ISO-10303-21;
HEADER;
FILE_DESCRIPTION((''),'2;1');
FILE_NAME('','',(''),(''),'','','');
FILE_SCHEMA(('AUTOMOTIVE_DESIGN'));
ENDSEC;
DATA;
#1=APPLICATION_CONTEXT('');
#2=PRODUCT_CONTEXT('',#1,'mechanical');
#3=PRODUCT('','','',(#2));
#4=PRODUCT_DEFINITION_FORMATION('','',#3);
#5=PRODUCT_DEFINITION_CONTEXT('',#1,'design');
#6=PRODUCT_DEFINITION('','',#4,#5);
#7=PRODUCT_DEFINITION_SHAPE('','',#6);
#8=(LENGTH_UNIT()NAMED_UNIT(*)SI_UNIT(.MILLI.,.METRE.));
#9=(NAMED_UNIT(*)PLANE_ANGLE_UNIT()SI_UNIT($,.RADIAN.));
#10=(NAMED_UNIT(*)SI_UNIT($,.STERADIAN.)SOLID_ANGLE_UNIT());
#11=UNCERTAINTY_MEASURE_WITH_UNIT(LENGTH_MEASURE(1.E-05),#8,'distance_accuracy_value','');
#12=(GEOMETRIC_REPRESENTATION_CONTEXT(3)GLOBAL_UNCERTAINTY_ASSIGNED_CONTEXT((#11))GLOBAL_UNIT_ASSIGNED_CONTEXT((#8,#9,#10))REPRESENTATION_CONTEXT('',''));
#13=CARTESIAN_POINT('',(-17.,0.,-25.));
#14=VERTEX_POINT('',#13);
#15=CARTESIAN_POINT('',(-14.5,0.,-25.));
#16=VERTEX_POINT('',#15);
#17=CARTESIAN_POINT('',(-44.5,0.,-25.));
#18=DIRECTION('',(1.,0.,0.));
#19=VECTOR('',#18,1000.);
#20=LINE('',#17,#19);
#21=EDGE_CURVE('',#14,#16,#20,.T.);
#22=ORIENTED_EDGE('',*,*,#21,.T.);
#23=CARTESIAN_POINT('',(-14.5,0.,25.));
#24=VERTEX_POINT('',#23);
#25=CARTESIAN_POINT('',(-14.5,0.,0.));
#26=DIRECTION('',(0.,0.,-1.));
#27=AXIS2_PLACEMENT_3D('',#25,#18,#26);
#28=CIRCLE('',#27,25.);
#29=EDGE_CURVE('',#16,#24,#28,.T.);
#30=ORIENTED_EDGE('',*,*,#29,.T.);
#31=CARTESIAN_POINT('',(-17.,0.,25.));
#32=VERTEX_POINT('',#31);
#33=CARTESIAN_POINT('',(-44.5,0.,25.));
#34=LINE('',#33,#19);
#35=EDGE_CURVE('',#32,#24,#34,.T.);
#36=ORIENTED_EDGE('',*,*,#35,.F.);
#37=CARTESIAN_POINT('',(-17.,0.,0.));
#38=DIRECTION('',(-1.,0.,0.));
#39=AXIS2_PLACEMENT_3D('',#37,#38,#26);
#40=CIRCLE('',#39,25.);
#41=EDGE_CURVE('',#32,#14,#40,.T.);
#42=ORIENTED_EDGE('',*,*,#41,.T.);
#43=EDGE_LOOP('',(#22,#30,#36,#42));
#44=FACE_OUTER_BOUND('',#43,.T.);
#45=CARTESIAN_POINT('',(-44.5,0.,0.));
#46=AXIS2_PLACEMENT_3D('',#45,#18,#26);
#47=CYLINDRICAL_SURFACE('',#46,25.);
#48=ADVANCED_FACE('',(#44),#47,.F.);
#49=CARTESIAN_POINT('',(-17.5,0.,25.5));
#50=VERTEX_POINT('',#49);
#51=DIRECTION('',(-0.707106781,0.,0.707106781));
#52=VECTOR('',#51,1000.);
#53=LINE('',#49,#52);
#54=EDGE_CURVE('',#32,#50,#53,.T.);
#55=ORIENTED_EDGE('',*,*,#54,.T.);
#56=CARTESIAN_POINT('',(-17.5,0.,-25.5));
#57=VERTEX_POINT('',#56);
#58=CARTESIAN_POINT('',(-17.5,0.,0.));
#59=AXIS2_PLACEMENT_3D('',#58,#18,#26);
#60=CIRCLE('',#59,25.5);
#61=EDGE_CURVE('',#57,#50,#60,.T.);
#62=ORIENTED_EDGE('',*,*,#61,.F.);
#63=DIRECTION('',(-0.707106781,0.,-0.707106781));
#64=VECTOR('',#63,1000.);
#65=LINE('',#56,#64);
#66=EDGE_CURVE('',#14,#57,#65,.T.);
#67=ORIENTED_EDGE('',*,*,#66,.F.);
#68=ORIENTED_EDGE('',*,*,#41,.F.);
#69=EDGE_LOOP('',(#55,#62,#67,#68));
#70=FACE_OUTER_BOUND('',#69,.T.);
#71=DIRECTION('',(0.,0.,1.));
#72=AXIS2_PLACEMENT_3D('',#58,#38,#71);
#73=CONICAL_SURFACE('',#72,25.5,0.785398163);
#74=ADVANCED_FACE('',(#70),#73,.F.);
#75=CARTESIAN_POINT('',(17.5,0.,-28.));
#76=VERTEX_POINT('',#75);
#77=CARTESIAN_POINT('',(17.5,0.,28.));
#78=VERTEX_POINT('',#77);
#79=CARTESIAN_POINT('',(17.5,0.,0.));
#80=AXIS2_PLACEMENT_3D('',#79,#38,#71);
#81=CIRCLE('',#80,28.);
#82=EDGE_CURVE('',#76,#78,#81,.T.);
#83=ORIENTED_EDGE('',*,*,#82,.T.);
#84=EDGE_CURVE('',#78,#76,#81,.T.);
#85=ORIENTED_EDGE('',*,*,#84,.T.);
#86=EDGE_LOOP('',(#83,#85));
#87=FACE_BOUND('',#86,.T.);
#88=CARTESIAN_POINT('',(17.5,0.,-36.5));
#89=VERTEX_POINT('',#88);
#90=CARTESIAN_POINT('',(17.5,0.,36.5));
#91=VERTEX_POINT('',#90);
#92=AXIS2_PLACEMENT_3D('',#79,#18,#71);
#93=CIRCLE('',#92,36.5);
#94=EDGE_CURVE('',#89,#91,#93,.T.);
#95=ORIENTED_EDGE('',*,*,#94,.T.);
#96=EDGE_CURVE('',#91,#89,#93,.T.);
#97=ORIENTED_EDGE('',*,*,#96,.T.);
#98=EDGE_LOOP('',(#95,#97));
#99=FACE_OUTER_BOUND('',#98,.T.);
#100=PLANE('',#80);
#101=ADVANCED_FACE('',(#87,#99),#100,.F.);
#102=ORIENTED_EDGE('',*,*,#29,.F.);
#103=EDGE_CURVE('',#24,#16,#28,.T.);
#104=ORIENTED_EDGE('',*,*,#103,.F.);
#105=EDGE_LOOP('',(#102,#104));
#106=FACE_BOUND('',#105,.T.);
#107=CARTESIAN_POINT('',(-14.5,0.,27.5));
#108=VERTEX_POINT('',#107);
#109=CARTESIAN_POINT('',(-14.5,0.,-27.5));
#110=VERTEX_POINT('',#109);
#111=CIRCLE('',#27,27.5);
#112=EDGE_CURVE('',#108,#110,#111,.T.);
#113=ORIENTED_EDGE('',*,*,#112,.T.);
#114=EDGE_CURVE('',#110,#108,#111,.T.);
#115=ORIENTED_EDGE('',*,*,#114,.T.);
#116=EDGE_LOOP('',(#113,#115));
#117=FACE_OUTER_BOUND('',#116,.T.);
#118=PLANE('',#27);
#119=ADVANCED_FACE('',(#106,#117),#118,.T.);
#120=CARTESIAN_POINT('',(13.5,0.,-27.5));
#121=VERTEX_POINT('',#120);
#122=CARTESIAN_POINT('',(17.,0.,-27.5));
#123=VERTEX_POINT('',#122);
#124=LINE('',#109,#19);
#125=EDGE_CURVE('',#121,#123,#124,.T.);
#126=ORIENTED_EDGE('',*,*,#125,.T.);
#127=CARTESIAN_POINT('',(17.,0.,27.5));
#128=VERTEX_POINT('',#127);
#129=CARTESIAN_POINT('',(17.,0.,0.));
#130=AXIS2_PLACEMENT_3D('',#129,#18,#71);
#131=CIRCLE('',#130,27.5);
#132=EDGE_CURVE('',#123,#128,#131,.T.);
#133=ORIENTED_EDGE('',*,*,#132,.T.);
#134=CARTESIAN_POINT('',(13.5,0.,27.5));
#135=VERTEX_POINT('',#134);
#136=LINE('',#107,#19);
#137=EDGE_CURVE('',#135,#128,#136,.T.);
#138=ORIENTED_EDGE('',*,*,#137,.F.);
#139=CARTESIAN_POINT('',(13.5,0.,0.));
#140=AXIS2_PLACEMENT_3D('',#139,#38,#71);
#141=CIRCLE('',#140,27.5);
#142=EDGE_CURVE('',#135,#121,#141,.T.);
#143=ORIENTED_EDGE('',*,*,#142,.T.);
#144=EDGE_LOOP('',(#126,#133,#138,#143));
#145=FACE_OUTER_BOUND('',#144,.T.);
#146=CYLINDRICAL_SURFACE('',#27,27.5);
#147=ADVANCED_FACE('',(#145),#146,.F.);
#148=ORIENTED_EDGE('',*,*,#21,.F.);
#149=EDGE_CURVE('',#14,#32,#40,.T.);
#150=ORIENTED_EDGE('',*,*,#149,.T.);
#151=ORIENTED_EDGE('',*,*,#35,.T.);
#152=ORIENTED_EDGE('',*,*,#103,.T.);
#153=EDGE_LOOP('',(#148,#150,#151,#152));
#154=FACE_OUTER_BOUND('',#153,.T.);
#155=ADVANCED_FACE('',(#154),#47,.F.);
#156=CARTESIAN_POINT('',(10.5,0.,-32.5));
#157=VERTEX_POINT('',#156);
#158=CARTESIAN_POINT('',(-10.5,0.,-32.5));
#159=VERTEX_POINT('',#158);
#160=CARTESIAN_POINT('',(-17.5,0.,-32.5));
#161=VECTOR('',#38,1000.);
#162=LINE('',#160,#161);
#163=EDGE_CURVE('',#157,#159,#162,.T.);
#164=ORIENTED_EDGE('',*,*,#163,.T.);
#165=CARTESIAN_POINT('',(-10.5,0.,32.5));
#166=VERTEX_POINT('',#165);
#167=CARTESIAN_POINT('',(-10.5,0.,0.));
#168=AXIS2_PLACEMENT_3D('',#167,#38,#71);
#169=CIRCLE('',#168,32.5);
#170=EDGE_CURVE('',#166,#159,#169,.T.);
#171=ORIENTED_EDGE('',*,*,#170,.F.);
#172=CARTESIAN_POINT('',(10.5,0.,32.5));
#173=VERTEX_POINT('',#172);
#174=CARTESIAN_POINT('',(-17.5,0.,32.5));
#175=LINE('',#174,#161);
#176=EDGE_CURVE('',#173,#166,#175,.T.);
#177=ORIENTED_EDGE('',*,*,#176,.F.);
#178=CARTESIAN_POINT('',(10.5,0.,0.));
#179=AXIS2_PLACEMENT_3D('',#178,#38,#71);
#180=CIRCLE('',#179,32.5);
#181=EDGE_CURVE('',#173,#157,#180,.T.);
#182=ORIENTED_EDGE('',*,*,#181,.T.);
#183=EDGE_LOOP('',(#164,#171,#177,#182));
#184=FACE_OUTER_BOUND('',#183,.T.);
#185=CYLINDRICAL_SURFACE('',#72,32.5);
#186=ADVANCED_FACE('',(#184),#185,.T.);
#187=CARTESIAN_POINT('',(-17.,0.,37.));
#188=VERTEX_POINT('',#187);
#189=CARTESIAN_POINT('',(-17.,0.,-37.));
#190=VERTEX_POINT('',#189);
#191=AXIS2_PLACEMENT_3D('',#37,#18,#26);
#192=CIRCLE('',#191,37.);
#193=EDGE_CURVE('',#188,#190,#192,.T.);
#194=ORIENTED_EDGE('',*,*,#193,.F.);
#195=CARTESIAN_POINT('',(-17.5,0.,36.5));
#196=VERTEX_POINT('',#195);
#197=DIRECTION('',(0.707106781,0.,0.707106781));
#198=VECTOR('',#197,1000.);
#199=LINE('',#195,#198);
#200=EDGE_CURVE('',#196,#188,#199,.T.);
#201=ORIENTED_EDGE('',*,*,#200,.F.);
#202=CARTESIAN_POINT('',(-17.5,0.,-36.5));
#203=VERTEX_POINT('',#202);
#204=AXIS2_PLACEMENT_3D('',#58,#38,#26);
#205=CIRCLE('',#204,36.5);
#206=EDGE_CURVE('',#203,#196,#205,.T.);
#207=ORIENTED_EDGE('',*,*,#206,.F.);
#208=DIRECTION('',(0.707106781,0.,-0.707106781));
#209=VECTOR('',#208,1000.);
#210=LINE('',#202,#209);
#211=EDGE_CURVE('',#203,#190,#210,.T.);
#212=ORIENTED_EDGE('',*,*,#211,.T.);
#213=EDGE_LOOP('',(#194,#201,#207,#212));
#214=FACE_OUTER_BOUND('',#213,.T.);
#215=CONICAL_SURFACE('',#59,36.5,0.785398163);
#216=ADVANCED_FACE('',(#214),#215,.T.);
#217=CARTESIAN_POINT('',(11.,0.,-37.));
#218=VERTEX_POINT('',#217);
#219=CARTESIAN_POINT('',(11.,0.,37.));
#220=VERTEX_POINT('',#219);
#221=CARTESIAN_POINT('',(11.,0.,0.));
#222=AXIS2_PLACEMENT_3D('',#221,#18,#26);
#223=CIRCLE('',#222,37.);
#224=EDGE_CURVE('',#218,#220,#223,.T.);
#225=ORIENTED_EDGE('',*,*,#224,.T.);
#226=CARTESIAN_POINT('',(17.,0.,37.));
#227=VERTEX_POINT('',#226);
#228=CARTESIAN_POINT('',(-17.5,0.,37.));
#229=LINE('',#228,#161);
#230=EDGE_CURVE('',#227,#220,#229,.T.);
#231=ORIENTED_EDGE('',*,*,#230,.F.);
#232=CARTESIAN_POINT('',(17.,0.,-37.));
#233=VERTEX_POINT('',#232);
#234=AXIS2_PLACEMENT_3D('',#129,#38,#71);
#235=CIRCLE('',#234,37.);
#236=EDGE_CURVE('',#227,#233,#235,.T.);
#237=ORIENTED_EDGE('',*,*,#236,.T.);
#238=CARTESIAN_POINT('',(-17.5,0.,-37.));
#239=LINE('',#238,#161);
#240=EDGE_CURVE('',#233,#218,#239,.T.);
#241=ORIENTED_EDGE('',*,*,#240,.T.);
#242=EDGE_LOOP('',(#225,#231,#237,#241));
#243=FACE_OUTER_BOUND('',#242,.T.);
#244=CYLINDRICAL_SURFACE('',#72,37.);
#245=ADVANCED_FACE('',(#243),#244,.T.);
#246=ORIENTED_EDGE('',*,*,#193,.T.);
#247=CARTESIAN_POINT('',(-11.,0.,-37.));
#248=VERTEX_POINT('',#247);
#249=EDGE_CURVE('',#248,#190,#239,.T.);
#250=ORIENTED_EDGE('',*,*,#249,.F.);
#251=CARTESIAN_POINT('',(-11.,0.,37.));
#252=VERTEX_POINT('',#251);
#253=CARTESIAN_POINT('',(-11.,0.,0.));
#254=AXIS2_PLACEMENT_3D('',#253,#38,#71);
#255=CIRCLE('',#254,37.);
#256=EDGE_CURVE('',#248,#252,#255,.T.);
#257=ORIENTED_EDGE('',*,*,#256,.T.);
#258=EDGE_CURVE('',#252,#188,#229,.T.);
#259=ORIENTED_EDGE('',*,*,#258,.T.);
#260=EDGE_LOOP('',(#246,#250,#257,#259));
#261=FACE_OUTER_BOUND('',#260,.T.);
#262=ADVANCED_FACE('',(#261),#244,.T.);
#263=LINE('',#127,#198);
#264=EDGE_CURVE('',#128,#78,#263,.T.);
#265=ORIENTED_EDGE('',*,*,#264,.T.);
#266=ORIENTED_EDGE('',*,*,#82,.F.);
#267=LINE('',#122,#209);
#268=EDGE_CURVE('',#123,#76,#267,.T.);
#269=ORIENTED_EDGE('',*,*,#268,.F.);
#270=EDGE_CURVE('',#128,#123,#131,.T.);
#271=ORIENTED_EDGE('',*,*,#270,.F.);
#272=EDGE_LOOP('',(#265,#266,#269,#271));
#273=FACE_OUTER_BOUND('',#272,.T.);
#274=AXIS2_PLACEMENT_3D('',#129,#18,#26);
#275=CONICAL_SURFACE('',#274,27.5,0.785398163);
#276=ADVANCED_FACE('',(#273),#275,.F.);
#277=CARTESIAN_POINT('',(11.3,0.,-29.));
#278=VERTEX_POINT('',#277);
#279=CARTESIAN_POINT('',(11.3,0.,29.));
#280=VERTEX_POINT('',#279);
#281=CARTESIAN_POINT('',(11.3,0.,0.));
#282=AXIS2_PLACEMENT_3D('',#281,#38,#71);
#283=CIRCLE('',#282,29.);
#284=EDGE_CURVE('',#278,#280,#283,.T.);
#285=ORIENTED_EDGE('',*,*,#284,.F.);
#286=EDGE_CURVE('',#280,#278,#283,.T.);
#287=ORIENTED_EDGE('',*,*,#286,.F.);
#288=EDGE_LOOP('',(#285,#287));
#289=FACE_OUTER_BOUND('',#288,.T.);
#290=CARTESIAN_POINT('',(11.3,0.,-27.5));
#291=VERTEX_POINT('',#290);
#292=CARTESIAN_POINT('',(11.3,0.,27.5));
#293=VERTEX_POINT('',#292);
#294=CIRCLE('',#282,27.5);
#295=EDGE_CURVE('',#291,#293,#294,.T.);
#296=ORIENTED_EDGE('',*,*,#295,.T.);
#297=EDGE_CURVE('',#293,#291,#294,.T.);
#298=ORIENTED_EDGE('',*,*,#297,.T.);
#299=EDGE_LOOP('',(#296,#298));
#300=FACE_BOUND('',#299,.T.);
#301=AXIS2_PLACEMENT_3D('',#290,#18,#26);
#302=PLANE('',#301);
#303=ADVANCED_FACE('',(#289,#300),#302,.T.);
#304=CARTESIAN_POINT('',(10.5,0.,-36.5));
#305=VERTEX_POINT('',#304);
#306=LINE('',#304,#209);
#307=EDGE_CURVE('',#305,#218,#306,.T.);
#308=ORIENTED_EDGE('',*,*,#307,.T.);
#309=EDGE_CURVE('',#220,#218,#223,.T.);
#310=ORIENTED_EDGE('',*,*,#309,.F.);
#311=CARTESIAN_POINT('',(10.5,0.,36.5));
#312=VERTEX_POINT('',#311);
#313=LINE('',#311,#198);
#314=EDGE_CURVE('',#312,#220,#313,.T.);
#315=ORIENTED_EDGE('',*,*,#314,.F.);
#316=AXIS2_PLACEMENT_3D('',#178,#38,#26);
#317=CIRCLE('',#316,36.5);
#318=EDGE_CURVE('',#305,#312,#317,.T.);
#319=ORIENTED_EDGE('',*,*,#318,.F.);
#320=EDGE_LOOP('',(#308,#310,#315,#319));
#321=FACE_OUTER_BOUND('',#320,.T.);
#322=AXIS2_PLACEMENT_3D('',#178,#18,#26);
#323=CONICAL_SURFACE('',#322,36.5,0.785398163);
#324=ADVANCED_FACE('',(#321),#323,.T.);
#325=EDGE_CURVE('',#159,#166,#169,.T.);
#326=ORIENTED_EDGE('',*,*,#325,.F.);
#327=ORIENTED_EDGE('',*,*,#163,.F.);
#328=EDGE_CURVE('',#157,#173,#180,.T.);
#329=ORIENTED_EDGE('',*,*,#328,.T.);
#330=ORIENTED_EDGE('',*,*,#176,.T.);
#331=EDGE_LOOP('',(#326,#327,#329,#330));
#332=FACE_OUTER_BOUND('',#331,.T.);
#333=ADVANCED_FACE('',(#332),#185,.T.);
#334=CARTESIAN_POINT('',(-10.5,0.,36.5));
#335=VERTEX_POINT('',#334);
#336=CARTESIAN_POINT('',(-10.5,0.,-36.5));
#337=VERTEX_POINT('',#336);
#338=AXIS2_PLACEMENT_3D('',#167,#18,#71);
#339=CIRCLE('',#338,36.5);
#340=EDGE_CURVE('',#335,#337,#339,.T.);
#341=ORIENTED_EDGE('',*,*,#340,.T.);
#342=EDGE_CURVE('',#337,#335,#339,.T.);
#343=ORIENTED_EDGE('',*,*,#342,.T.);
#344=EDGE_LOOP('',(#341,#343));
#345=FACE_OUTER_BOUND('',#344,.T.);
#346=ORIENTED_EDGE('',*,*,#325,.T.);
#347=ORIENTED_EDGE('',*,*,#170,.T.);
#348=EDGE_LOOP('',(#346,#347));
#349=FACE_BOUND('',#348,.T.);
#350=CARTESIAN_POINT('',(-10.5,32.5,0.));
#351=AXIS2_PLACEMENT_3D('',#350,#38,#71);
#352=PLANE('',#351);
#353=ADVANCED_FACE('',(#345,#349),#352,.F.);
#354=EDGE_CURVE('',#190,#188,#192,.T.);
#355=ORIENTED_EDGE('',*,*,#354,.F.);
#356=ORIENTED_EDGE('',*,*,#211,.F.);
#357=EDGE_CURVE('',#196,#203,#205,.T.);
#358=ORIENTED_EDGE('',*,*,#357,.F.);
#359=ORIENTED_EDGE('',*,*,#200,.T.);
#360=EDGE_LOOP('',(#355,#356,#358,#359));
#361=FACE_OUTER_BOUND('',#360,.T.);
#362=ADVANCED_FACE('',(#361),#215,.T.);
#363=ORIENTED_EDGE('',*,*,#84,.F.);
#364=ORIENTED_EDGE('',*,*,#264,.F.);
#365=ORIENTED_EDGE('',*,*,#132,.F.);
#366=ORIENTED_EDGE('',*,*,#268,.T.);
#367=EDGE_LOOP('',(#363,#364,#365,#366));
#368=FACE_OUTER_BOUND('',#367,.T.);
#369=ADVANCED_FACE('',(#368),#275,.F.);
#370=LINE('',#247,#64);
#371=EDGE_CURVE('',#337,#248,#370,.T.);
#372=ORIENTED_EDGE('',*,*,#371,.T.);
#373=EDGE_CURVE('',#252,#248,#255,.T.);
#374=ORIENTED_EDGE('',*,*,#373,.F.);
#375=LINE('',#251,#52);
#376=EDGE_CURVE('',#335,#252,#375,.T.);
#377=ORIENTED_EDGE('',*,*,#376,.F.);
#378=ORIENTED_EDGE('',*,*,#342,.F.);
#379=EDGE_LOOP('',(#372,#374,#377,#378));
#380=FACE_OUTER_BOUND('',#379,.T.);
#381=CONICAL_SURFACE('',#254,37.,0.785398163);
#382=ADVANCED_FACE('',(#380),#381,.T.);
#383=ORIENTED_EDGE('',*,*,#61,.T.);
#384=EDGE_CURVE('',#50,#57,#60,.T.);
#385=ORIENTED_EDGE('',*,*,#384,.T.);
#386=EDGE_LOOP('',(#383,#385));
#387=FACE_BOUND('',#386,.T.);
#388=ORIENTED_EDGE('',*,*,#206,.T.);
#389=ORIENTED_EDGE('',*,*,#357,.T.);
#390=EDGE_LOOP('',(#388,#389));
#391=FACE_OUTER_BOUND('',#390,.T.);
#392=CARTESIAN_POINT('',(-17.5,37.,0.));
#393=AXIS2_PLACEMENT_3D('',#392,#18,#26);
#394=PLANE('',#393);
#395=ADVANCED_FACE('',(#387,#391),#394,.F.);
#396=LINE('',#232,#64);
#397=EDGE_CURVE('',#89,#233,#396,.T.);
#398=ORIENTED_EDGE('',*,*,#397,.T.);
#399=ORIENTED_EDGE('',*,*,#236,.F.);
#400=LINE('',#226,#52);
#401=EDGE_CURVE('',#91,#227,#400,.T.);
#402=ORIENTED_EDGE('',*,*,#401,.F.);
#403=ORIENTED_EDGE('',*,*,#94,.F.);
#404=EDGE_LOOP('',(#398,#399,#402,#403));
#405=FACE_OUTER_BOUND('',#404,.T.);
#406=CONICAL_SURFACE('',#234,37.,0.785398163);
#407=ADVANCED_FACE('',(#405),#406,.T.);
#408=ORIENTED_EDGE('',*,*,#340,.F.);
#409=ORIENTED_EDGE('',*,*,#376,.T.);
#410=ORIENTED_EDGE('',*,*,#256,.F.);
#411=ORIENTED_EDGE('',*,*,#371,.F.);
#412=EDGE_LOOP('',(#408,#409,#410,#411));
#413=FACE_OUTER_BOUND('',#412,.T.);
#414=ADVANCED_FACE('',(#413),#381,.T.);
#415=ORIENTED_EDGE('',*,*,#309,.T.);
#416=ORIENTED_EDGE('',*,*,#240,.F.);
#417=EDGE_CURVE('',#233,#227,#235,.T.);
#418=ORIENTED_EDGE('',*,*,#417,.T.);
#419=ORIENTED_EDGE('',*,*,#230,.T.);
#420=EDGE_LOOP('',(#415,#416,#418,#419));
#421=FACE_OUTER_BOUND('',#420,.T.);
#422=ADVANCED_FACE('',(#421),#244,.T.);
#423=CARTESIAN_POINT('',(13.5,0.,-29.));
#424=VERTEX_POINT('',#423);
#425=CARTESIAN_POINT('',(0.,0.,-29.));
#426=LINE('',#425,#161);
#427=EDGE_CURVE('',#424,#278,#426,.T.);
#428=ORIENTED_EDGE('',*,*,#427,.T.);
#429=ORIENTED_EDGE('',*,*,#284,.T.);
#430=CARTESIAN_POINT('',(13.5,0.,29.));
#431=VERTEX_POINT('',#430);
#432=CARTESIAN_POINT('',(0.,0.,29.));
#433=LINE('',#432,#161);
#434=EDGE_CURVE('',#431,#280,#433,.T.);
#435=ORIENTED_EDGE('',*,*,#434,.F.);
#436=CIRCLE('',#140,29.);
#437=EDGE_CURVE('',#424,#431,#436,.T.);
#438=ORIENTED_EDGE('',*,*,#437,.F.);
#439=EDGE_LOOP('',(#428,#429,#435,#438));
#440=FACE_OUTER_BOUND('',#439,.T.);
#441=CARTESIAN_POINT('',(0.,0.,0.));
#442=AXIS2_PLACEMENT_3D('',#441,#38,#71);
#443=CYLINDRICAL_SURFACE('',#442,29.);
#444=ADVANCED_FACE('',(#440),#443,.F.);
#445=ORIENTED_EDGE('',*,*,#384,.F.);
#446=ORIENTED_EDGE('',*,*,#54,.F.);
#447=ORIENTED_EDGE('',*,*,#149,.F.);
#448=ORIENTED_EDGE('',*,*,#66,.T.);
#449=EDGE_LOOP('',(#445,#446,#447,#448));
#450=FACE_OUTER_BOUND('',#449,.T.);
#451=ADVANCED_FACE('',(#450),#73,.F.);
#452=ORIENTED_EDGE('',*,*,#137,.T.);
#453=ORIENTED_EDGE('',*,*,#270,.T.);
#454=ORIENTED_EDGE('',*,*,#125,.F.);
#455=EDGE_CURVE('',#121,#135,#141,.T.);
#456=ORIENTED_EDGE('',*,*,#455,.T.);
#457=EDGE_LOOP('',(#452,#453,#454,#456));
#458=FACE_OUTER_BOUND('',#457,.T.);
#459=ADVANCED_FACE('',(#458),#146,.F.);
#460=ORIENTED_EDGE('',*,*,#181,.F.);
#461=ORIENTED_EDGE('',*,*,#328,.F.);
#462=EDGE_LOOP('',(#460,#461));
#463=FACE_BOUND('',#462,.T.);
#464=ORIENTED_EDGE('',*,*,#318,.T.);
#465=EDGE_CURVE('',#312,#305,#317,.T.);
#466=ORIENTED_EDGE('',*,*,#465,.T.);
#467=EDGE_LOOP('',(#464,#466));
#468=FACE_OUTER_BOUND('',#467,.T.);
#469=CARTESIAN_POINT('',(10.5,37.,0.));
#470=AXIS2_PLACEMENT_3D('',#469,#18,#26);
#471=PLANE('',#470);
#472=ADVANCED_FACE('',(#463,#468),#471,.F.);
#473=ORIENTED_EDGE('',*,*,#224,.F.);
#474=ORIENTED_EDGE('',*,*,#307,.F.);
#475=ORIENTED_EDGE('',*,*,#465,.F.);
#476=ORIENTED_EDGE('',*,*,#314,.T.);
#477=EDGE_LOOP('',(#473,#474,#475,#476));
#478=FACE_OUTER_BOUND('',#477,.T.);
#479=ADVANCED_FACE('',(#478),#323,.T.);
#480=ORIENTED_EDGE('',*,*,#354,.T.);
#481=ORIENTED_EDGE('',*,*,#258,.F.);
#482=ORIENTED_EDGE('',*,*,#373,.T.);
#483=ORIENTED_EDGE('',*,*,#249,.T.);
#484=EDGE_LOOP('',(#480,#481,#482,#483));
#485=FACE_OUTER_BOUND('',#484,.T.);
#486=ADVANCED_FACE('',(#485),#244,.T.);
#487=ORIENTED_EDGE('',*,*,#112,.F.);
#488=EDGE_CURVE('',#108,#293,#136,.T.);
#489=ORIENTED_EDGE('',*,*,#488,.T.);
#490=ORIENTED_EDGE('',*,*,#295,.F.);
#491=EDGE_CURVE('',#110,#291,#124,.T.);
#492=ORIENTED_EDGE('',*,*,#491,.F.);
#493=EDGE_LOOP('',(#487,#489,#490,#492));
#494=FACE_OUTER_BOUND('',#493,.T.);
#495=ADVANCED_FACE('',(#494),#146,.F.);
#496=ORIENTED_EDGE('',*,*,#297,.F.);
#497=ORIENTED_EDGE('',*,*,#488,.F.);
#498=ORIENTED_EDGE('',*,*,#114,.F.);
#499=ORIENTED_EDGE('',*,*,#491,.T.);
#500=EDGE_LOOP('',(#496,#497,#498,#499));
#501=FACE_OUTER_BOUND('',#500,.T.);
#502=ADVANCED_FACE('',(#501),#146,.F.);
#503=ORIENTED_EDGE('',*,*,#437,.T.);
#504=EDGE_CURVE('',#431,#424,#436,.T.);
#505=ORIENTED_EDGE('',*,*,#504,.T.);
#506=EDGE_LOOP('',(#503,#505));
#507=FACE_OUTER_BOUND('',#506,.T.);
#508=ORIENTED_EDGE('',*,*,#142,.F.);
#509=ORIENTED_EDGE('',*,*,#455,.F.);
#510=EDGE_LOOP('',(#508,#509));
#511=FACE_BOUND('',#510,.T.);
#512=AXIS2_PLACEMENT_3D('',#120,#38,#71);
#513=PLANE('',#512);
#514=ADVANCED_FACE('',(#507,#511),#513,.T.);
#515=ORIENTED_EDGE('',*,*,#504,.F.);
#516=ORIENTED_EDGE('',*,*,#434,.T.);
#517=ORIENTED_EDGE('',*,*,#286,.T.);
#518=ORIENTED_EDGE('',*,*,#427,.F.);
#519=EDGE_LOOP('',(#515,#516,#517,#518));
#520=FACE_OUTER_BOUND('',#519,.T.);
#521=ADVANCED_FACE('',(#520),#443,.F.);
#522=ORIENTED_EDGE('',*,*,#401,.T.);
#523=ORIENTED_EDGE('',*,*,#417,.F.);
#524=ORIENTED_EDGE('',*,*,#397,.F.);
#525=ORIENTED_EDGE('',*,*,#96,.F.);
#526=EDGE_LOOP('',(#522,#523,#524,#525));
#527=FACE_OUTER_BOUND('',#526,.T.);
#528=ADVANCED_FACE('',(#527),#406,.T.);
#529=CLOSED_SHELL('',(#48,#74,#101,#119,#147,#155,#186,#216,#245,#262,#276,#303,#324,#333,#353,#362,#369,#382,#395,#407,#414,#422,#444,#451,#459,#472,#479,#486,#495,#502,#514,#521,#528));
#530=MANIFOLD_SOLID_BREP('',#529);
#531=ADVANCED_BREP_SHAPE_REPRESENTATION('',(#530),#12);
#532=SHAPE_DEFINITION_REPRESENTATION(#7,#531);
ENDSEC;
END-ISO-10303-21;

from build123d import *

# Parameters (mm, degrees)
SKETCH_2_R          = 27.5
CUT_EXTRUDE_1_DEPTH = 32
SKETCH_4_R          = 25
CUT_EXTRUDE_2_DEPTH = 30
CHAMFER_1_SIZE      = 0.5
SKETCH_5_W          = 2.2
SKETCH_5_H          = 1.5


with BuildPart() as part:
    # 草图1 → 旋转1 (revolve)
    with BuildSketch(Plane.XY, mode=Mode.PRIVATE) as revolve_1_sk:
        Polygon((-17.5, 0), (17.5, 0), (17.5, 37), (10.5, 37), (10.5, 32.5), (-10.5, 32.5), (-10.5, 37), (-17.5, 37), align=None)
    revolve(revolve_1_sk.sketch.rotate(Axis((-17.5, 0, 0), (1, 0, 0)), 90), axis=Axis((-17.5, 0, 0), (1, 0, 0)))

    # 草图2 → 切除-拉伸1 (cut)
    with BuildSketch(Plane(origin=(17.5, 0, 0), x_dir=(0, 0, -1), z_dir=(1, 0, 0))):
        Circle(SKETCH_2_R)
    extrude(amount=-CUT_EXTRUDE_1_DEPTH, mode=Mode.SUBTRACT)

    # 草图4 → 切除-拉伸2 (cut)
    with BuildSketch(Plane(origin=(-14.5, 0, 0), x_dir=(0, 0, -1), z_dir=(1, 0, 0))):
        Circle(SKETCH_4_R)
    extrude(amount=-CUT_EXTRUDE_2_DEPTH, mode=Mode.SUBTRACT)

    # 倒角1
    chamfer_1_edges = [part.edges().sort_by_distance(p)[0] for p in [
        (17.5, 0, 27.5),
        (-17.5, 0, 25),
        (-17.5, 0, -37),
        (-10.5, 0, -37),
        (10.5, 0, -37),
        (17.5, 0, -37),
    ]]
    chamfer(chamfer_1_edges, length=CHAMFER_1_SIZE)

    # 草图5 → 切除-旋转1 (revolve, cut)
    with BuildSketch(Plane(origin=(0, 0, 0), x_dir=(1, 0, 0), z_dir=(0, 1, 0))):
        with Locations((12.4, 28.25)):
            Rectangle(SKETCH_5_W, SKETCH_5_H)
    revolve(axis=Axis((0, 0, 0), (1, 0, 0)), mode=Mode.SUBTRACT)


solid = part.part
